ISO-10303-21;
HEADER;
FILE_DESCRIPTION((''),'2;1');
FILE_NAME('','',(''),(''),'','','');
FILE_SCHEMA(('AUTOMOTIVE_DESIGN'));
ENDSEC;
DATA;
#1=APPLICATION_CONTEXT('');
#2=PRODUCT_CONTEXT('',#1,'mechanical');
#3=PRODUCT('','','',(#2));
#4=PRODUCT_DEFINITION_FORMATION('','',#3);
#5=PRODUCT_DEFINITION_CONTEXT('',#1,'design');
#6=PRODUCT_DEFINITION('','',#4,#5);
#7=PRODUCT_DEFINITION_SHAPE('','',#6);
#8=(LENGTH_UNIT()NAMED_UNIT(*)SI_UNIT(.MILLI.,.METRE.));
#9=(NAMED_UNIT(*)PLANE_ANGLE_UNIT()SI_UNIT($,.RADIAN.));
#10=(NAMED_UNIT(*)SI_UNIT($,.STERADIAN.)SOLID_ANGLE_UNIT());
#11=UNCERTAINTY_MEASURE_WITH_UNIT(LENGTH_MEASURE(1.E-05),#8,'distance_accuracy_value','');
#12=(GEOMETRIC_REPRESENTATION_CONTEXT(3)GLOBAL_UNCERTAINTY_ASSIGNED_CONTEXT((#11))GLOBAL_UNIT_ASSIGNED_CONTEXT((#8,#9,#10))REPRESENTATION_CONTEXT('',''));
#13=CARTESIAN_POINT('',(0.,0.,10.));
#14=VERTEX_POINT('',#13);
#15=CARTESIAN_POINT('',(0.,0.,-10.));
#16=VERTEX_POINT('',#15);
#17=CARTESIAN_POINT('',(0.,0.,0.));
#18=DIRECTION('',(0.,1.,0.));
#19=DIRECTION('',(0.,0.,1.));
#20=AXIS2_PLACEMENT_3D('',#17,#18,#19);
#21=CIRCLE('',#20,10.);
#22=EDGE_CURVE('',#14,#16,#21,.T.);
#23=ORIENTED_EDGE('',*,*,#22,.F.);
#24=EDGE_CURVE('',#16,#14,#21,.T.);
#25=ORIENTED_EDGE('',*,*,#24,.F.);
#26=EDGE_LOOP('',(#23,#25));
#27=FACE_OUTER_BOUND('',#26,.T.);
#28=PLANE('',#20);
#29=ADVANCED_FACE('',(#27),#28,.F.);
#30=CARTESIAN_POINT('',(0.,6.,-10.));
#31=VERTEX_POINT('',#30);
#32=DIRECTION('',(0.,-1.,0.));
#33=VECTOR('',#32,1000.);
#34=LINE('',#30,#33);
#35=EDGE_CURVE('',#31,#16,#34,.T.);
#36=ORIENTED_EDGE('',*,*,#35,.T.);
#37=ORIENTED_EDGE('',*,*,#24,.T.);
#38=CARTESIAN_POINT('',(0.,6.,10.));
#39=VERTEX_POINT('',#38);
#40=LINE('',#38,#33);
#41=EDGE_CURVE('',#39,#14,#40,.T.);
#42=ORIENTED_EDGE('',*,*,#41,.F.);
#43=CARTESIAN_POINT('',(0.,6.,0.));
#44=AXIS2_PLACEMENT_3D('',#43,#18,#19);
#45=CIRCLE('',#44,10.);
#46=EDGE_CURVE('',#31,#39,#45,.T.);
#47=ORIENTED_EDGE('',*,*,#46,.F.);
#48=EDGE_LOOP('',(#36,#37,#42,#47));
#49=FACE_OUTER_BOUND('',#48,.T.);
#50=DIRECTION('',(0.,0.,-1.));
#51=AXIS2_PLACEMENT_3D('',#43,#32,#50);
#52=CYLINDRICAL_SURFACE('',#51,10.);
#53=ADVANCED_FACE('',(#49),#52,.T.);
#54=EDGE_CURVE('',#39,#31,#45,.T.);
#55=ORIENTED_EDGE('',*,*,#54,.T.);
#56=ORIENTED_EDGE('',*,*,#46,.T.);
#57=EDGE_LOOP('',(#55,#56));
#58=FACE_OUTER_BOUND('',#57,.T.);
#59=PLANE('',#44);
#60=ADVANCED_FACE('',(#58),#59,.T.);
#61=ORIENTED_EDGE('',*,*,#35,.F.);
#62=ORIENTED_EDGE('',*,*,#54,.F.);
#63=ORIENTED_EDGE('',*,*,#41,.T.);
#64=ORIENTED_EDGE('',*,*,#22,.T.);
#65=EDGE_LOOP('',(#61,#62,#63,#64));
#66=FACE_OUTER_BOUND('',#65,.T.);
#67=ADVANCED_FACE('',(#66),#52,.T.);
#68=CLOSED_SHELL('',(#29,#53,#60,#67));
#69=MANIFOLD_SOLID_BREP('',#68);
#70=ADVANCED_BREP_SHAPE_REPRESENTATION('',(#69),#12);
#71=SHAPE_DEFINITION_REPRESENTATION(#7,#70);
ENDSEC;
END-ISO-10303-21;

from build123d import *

# Parameters (mm, degrees)
SKETCH1_R           = 10
BOSS_EXTRUDE1_DEPTH = 6


with BuildPart() as part:
    # Sketch1 → Boss-Extrude1 (new body)
    with BuildSketch(Plane(origin=(0, 0, 0), x_dir=(1, 0, 0), z_dir=(0, 1, 0))):
        with Locations(Location((0, 0, 0), (0, 0, 270))):
            Circle(SKETCH1_R)
    extrude(amount=BOSS_EXTRUDE1_DEPTH)


solid = part.part
